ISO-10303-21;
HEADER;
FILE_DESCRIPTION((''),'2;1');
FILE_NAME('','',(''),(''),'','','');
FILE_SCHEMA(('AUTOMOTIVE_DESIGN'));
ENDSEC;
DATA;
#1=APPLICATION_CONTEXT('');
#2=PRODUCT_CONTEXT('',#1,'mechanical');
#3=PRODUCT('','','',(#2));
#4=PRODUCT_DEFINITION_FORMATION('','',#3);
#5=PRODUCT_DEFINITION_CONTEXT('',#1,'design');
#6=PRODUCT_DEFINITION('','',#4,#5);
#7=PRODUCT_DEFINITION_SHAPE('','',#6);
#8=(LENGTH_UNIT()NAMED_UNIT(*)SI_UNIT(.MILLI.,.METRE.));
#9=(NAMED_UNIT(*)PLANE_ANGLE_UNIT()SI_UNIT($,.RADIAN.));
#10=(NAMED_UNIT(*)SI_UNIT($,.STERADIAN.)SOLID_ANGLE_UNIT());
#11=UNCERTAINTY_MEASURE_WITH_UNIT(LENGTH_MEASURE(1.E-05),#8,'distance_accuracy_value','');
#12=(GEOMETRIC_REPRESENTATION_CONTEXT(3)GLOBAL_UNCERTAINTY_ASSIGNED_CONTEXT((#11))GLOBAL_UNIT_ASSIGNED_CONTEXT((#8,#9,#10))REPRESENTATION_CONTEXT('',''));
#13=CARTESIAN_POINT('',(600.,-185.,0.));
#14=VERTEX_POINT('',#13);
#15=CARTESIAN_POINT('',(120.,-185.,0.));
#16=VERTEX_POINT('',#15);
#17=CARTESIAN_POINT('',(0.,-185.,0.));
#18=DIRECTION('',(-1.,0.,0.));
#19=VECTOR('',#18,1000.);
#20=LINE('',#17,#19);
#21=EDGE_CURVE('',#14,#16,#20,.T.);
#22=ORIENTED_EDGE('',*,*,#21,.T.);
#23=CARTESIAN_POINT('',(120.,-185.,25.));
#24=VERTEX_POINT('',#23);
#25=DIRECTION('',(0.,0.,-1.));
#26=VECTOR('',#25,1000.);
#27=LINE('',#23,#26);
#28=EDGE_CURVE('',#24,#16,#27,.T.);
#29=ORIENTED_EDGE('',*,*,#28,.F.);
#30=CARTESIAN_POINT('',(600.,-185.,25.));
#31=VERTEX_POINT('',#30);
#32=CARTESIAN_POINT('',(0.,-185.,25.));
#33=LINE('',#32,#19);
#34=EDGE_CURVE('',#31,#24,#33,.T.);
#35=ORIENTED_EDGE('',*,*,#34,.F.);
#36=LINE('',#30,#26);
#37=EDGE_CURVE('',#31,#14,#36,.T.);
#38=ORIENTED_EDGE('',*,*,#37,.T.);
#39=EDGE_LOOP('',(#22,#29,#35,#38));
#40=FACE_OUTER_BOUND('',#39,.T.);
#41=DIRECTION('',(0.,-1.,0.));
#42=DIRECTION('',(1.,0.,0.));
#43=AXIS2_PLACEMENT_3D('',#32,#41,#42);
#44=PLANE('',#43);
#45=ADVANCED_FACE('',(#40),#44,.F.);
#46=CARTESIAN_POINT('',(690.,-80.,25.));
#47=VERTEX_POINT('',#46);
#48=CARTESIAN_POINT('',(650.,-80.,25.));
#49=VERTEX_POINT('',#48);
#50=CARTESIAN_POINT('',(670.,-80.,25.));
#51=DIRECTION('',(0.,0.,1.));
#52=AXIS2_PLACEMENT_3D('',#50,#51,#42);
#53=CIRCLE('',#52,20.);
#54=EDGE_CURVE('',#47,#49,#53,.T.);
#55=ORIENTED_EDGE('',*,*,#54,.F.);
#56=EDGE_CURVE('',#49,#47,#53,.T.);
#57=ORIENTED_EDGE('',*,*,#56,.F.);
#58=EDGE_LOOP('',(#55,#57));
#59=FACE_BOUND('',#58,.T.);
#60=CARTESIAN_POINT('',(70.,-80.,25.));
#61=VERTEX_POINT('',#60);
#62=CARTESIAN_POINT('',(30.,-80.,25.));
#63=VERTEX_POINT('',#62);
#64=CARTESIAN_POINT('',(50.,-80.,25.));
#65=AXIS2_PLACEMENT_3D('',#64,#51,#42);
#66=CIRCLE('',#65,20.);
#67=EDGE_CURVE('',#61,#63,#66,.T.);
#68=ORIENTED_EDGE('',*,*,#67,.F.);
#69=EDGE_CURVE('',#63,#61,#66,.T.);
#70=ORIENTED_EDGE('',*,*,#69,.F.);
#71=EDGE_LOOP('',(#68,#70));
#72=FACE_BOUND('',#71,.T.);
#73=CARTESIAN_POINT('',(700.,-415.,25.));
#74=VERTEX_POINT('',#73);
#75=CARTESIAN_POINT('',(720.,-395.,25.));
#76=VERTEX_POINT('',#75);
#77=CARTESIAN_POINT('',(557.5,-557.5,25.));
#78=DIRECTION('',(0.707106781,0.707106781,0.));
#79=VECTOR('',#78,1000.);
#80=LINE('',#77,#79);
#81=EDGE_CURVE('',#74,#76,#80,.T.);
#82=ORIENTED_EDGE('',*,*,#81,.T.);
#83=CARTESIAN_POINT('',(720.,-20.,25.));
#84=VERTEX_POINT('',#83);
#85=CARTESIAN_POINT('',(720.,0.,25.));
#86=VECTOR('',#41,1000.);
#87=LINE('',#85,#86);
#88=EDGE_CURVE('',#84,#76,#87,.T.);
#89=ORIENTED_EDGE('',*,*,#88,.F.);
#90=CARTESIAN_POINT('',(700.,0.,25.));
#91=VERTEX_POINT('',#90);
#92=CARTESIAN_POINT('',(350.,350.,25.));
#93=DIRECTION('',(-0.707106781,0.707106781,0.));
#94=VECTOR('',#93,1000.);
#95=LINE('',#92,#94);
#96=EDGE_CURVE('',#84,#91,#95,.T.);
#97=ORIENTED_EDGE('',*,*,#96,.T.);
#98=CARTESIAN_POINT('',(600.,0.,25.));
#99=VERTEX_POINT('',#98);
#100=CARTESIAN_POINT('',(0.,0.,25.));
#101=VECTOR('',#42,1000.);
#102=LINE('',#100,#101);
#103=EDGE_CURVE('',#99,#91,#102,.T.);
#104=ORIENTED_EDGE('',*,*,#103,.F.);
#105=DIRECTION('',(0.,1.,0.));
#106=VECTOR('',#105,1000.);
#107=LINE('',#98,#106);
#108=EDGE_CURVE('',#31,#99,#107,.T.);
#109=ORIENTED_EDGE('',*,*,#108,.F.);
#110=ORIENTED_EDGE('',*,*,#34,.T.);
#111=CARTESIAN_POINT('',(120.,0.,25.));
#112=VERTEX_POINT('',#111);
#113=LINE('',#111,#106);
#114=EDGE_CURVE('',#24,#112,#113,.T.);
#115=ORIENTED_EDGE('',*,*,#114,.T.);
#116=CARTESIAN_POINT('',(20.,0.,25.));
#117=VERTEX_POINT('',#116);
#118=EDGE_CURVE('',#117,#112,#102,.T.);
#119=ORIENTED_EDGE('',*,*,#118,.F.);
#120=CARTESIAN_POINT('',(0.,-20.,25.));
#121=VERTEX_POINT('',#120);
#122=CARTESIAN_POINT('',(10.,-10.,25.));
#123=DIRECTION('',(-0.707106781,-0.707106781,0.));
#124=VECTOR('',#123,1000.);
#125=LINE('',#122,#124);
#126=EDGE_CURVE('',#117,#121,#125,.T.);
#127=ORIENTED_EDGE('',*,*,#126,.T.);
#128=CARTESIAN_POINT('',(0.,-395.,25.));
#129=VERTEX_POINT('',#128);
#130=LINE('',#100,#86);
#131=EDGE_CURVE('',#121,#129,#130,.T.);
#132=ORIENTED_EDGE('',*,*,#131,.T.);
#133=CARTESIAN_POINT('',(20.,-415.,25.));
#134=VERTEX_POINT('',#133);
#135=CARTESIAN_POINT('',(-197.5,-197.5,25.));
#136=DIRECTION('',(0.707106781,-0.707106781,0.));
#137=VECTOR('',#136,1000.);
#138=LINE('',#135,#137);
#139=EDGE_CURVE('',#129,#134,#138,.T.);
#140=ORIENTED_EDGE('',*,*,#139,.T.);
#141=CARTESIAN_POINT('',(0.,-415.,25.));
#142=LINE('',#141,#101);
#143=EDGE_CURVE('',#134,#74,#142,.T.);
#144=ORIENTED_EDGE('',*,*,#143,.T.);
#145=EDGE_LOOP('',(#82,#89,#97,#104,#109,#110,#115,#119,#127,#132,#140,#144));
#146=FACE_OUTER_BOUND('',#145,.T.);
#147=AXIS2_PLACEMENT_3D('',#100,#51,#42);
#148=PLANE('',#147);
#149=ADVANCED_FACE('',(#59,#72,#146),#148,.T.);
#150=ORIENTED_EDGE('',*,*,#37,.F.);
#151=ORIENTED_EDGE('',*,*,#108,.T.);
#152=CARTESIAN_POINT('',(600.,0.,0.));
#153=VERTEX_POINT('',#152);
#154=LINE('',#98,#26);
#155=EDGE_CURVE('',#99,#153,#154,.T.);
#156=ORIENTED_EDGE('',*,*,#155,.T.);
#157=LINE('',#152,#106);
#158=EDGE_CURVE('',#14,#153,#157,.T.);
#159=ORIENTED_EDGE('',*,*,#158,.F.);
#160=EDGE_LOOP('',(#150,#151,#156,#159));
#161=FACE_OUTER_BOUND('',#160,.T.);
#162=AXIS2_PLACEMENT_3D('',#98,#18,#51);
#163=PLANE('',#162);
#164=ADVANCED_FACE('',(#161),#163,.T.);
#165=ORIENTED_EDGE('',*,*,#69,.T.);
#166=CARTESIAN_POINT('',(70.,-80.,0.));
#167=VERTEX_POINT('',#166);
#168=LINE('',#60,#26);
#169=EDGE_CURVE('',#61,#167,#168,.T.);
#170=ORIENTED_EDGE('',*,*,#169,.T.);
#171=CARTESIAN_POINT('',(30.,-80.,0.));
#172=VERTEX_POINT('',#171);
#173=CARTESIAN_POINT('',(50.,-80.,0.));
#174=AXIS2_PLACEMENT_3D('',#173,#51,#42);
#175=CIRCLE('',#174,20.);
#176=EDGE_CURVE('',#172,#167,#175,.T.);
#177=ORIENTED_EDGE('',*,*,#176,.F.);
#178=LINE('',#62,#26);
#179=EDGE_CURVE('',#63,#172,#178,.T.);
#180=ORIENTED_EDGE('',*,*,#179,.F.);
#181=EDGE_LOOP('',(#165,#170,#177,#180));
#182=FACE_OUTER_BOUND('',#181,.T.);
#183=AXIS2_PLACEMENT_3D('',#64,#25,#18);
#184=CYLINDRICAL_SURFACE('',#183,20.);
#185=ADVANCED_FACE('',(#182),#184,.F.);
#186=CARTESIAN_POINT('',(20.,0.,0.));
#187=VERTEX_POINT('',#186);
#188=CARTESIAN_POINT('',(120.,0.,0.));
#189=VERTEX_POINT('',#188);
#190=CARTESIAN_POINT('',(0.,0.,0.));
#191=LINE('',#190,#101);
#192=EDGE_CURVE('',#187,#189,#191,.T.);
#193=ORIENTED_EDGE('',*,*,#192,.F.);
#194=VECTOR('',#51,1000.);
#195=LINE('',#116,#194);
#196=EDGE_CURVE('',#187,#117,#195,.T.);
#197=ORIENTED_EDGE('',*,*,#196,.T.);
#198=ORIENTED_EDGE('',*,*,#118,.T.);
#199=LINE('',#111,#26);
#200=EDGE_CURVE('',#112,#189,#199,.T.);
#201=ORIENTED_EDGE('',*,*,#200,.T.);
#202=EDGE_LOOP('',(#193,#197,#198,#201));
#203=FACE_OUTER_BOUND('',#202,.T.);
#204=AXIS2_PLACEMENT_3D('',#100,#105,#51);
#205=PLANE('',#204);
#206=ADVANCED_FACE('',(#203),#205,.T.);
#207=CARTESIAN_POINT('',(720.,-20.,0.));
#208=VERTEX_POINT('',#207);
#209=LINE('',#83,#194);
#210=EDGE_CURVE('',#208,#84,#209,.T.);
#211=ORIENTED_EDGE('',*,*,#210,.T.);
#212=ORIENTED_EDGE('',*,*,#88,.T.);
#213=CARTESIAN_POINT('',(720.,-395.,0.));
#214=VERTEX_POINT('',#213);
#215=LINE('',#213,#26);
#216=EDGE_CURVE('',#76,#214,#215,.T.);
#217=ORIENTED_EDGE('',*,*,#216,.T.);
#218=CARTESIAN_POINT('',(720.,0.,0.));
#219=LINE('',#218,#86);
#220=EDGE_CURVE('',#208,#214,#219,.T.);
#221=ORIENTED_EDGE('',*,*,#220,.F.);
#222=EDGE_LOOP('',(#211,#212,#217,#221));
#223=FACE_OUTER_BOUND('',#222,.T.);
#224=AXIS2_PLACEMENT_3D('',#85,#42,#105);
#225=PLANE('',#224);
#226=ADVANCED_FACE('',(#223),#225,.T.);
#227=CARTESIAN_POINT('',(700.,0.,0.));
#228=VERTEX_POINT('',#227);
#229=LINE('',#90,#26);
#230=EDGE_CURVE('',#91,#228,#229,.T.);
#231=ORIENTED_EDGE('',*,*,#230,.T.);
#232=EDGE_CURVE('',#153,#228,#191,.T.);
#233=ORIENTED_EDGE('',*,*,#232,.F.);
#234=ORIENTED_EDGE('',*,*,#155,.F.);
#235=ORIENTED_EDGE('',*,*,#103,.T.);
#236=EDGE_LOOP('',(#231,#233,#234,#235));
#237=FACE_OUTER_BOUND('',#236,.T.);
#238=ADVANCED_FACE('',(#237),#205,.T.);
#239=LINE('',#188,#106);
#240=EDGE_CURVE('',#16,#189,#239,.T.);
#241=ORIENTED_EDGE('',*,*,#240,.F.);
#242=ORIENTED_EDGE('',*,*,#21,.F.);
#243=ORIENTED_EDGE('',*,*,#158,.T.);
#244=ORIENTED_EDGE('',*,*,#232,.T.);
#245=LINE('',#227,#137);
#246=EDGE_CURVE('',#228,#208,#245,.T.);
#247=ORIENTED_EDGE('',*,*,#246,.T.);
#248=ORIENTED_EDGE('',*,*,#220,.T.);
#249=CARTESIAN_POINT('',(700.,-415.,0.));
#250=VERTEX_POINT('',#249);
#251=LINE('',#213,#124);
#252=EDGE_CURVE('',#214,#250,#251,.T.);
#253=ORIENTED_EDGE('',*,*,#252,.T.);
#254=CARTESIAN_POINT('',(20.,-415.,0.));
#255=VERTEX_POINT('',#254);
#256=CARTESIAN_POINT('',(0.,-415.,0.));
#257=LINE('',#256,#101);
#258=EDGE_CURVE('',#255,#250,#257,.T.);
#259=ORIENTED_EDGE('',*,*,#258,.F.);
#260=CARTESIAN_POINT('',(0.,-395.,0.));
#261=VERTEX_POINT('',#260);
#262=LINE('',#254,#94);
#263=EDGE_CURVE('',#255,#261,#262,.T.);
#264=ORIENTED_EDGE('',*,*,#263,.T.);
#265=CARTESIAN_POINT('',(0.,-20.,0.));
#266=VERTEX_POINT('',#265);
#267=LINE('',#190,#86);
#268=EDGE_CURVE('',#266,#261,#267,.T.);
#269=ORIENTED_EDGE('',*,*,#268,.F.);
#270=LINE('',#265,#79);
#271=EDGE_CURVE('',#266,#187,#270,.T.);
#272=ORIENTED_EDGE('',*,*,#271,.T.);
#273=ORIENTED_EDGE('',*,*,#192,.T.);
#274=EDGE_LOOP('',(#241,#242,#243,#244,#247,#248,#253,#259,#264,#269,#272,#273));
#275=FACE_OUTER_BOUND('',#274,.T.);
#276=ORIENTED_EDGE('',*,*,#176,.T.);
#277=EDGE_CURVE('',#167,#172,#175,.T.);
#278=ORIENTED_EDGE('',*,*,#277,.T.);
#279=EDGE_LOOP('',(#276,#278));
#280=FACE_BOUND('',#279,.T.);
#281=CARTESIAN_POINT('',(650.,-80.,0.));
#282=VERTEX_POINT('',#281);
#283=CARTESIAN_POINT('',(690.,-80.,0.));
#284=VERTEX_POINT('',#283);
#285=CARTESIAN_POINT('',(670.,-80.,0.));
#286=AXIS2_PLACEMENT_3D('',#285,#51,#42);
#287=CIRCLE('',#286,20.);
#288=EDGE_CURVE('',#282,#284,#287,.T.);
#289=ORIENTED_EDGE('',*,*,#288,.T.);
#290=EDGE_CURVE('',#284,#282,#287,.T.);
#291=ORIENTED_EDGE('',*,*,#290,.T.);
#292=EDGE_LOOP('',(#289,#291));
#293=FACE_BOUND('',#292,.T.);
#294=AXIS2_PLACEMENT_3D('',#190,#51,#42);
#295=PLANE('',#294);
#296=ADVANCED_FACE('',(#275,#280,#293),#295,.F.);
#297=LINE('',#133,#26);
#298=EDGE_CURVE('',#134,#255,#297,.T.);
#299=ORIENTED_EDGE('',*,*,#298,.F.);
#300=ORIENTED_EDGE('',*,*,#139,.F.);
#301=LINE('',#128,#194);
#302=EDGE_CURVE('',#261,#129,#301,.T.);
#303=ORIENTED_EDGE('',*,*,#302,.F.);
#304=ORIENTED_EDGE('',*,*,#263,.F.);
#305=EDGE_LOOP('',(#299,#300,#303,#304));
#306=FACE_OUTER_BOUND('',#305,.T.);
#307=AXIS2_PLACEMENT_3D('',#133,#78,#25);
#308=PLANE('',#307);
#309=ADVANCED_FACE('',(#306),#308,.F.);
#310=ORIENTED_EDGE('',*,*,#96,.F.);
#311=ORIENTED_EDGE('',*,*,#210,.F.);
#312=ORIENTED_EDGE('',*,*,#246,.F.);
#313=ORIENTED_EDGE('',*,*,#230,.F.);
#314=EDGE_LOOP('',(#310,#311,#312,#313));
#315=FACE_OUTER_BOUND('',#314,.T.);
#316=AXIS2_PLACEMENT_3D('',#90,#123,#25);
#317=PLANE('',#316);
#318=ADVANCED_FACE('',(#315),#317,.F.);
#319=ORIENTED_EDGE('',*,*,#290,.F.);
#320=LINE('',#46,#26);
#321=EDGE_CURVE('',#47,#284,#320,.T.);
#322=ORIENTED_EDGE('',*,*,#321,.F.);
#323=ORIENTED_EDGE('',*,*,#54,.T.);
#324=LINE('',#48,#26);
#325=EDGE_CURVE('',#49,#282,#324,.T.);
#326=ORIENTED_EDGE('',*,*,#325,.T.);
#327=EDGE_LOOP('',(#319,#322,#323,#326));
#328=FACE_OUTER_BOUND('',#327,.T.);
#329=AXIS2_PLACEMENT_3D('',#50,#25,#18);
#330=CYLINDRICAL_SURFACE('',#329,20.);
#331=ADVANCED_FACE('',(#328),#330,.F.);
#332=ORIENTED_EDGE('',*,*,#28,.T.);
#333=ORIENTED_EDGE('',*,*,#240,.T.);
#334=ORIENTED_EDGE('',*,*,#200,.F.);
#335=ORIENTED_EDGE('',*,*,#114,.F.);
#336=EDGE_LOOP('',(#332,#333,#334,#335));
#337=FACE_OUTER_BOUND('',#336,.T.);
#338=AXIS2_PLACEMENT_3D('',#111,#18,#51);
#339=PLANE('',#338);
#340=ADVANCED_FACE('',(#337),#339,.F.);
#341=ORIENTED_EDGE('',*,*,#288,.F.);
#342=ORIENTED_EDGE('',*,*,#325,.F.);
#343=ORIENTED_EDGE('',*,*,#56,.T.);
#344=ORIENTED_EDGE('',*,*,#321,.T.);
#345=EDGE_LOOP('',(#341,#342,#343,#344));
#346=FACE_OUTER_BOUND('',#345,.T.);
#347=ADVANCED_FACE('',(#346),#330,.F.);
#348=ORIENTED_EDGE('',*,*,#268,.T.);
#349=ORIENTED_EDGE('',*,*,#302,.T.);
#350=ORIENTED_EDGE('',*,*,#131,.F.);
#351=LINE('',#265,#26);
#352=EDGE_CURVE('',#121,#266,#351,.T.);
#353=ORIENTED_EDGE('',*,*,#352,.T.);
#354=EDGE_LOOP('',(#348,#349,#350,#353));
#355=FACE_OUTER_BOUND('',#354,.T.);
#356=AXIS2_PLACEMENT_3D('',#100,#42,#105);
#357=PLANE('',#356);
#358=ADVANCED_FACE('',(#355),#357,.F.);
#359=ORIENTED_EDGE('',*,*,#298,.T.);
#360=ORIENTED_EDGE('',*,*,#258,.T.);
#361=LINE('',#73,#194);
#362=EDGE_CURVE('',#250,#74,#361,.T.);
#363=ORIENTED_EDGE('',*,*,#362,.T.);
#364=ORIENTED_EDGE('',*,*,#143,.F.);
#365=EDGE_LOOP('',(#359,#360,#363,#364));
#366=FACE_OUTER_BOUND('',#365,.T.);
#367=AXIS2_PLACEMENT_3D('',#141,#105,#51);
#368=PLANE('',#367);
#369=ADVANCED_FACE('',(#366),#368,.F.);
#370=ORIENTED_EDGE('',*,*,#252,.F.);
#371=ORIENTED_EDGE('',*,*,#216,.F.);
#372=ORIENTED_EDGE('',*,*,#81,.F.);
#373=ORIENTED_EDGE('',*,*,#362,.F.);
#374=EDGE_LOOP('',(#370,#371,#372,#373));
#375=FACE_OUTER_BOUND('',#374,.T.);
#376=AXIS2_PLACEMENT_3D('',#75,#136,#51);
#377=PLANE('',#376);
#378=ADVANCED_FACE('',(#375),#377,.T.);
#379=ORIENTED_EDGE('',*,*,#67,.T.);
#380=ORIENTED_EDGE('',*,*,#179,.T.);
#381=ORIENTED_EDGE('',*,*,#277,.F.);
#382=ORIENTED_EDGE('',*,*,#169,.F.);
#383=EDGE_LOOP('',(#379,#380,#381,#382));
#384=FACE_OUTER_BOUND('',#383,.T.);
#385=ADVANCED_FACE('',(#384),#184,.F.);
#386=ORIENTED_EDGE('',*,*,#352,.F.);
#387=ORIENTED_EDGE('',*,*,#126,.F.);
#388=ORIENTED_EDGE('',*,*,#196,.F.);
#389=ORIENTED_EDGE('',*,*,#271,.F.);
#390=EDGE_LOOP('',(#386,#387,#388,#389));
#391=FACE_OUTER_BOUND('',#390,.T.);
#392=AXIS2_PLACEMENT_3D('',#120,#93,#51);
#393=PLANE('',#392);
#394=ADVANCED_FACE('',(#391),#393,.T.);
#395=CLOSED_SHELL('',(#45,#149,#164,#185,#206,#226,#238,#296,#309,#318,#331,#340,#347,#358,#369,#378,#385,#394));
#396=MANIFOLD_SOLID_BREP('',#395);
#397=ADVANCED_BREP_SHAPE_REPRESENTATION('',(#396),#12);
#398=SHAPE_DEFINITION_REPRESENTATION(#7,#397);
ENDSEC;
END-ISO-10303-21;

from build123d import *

# Parameters (mm, degrees)
SKETCH1_R           = 20
BOSS_EXTRUDE1_DEPTH = 25
CHAMFER1_SIZE       = 20


with BuildPart() as part:
    # Sketch1 → Boss-Extrude1 (new body)
    with BuildSketch(Plane.XY):
        Polygon((120, 0), (0, 0), (0, -415), (720, -415), (720, 0), (600, 0), (600, -185), (120, -185), align=None)
        with Locations((50, -80)):
            Circle(SKETCH1_R, mode=Mode.SUBTRACT)
        with Locations((670, -80)):
            Circle(SKETCH1_R, mode=Mode.SUBTRACT)
    extrude(amount=BOSS_EXTRUDE1_DEPTH)

    # Chamfer1
    chamfer1_edges = [part.edges().sort_by_distance(p)[0] for p in [
        (720, 0, 12.5),
        (720, -415, 12.5),
        (0, -415, 12.5),
        (0, 0, 12.5),
    ]]
    chamfer(chamfer1_edges, length=CHAMFER1_SIZE)


solid = part.part
